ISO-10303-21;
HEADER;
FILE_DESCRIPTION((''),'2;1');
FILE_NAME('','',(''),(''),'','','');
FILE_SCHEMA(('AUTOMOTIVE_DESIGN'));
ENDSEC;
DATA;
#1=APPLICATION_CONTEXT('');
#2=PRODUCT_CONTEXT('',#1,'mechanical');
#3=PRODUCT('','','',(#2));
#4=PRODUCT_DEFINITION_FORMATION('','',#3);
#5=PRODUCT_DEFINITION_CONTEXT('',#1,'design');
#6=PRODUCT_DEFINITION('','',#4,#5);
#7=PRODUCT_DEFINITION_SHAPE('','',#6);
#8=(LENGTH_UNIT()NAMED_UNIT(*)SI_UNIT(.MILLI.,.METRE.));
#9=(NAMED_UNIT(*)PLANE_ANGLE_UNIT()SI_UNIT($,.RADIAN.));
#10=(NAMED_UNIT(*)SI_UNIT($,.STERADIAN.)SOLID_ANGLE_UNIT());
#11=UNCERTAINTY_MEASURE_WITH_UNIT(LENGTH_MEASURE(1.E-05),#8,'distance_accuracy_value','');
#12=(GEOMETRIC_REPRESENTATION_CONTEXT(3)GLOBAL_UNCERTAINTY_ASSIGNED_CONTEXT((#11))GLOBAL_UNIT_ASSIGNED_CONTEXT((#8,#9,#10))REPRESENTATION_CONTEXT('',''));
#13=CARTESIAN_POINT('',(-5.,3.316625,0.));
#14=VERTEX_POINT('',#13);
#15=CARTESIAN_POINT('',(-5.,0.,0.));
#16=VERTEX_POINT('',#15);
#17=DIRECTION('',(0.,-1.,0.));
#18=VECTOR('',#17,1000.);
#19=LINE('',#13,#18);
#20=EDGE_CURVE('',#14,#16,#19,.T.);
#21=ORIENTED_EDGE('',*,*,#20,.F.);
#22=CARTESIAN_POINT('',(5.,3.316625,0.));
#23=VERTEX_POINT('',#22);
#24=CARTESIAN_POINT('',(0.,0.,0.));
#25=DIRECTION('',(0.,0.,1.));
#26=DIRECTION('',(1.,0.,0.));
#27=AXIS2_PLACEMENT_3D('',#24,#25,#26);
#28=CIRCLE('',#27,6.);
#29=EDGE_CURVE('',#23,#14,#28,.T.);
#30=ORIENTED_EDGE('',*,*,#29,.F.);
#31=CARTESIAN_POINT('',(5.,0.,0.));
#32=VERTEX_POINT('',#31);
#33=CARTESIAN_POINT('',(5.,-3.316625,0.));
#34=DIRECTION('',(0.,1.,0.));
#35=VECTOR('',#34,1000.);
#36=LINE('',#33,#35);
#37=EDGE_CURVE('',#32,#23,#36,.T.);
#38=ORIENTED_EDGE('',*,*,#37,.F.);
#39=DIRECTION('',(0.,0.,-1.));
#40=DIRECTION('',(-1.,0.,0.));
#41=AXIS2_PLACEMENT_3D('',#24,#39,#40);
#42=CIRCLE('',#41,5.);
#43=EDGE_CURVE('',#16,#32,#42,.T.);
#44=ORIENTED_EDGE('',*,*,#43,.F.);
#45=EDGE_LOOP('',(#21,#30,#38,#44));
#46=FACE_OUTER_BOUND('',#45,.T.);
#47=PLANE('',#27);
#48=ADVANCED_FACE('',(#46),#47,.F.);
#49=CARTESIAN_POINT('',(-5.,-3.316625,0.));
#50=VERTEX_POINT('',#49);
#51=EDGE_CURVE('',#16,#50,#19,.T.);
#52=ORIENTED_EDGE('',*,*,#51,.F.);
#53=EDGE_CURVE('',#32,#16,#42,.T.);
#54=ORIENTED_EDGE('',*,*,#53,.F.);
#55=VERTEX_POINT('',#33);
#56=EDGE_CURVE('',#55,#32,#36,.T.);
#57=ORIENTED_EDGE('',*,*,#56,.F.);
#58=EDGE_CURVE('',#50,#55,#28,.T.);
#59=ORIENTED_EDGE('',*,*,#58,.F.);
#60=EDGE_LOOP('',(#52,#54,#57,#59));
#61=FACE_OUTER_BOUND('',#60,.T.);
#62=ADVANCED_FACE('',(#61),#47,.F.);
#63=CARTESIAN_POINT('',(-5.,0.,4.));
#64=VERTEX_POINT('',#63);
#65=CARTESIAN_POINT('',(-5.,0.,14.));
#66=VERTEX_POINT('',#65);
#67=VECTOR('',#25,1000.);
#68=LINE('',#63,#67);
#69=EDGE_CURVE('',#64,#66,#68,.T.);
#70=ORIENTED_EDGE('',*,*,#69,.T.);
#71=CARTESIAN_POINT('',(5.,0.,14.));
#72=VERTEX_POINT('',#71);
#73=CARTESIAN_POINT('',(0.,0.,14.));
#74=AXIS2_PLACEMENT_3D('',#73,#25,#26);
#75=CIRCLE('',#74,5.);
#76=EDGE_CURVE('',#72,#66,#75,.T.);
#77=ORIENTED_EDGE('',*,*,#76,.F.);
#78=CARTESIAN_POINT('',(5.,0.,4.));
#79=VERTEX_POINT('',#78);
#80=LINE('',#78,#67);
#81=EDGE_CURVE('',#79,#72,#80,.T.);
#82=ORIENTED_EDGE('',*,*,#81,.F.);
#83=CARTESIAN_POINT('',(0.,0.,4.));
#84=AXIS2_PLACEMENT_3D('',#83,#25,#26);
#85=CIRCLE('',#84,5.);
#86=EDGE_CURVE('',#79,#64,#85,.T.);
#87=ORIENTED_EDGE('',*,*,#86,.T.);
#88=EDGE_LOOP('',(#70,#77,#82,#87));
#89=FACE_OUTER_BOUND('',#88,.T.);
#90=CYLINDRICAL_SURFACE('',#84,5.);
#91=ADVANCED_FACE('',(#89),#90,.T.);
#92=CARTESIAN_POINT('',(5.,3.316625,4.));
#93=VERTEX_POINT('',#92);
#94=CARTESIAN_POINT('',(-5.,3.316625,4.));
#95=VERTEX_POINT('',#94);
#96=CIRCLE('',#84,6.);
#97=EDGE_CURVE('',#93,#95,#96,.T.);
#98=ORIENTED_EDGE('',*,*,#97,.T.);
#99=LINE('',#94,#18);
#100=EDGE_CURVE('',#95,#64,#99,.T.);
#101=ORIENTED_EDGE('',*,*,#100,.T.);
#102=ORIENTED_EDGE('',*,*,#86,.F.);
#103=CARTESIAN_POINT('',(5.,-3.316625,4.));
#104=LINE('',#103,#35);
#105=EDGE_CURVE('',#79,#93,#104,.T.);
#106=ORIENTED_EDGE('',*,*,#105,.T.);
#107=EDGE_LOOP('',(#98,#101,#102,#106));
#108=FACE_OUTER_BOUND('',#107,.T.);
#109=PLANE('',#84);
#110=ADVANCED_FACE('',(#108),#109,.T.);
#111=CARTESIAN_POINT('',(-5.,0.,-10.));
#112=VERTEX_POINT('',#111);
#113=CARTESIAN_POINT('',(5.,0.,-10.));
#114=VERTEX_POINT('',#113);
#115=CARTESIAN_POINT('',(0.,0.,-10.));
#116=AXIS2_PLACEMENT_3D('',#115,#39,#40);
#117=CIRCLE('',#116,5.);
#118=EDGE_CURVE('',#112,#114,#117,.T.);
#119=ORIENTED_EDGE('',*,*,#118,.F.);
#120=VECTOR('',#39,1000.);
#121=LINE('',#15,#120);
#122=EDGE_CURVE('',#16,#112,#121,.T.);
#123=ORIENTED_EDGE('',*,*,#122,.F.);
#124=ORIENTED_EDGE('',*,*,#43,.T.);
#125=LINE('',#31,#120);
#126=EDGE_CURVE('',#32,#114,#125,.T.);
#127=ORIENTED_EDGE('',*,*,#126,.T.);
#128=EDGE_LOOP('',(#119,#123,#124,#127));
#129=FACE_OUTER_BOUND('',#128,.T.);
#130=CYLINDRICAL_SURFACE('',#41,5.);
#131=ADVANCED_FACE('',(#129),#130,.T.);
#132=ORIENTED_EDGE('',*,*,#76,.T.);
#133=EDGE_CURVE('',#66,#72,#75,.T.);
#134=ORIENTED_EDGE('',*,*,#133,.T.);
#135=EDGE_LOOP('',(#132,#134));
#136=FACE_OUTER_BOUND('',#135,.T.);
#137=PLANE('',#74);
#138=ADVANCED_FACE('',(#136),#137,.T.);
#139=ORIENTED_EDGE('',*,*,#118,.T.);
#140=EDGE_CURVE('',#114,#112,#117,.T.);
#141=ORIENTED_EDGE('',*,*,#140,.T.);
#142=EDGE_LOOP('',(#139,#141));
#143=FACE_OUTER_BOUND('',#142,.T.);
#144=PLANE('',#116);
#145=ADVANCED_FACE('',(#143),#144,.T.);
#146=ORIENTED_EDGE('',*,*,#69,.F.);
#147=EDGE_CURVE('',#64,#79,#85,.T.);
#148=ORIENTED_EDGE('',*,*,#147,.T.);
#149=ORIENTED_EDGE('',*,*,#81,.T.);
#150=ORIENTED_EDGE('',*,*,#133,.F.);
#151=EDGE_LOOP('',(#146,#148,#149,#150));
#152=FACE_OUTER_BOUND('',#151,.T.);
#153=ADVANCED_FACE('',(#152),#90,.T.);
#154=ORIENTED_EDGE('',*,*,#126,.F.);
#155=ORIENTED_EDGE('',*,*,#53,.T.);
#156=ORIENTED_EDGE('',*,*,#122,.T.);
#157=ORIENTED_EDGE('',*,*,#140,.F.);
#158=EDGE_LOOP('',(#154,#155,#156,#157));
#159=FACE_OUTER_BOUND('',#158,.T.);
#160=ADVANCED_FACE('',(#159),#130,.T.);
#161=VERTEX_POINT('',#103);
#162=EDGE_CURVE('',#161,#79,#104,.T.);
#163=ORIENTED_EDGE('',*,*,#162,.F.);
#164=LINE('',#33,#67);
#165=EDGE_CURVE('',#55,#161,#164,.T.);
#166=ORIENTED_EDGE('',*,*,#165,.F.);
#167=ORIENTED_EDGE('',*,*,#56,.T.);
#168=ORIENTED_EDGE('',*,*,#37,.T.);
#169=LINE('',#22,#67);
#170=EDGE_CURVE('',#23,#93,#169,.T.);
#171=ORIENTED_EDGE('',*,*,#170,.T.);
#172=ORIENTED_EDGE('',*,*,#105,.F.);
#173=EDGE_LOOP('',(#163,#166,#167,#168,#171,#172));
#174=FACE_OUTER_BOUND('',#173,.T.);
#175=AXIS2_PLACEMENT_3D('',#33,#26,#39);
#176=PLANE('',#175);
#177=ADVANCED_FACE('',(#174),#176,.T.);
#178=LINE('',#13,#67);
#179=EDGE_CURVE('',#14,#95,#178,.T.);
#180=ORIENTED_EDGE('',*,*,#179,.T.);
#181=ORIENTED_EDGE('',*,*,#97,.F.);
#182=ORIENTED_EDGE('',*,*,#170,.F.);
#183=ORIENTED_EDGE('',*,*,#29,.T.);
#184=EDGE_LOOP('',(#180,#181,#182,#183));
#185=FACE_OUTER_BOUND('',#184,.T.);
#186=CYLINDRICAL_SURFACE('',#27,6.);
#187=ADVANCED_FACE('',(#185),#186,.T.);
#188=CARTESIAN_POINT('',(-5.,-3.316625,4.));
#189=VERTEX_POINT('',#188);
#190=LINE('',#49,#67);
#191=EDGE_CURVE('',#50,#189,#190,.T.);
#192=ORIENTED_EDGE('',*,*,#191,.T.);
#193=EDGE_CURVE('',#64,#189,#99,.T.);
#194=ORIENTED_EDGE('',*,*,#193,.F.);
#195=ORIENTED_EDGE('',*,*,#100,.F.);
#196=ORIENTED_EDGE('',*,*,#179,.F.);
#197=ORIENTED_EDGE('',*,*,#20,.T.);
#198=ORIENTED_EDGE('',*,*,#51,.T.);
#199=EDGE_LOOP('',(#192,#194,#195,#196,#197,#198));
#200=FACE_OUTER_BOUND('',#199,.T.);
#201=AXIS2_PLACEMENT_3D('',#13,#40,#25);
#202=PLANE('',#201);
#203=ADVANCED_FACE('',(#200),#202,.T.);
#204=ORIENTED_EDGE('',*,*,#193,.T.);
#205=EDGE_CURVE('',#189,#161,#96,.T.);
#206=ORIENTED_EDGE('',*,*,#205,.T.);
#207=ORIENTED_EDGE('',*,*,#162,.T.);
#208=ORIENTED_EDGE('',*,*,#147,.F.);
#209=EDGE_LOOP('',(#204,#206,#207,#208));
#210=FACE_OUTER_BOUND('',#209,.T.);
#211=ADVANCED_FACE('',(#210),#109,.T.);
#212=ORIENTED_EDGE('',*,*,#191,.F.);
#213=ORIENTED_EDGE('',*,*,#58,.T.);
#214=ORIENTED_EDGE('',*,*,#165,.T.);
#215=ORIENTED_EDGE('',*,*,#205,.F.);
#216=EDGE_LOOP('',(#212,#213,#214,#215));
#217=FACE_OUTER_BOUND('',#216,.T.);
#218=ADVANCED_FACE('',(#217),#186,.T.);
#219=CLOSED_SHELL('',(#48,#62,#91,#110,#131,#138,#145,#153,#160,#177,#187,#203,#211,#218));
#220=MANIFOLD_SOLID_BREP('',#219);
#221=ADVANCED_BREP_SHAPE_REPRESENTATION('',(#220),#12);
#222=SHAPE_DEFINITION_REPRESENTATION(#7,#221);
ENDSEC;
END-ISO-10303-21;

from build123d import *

# Parameters (mm, degrees)
BOSS_EXTRUDE1_DEPTH = 4
SKETCH2_W           = 5
SKETCH2_H           = 10
SKETCH3_W           = 5
SKETCH3_H           = 10


with BuildPart() as part:
    # Sketch1 → Boss-Extrude1 (new body)
    with BuildSketch(Plane.XY.offset(4)):
        with BuildLine():
            Line((5, -3.31662479), (5, 3.31662479))
            ThreePointArc((5, 3.31662479), (0, 6), (-5, 3.31662479))
            Line((-5, 3.31662479), (-5, -3.31662479))
            ThreePointArc((-5, -3.31662479), (0, -6), (5, -3.31662479))
        make_face()
    extrude(amount=-BOSS_EXTRUDE1_DEPTH)

    # Sketch2 → Revolve1 (revolve)
    with BuildSketch(Plane(origin=(0, 0, 0), x_dir=(1, 0, 0), z_dir=(0, 1, 0))):
        with Locations((2.5, -9)):
            Rectangle(SKETCH2_W, SKETCH2_H)
    revolve(axis=Axis((0, 0, 4), (0, 0, 1)))

    # Sketch3 → Revolve2 (revolve)
    with BuildSketch(Plane.XZ, mode=Mode.PRIVATE) as revolve2_sk:
        with Locations((2.5, -5)):
            Rectangle(SKETCH3_W, SKETCH3_H)
    revolve(revolve2_sk.sketch.rotate(Axis((0, 0, 0), (0, 0, -1)), 180), axis=Axis((0, 0, 0), (0, 0, -1)))


solid = part.part
